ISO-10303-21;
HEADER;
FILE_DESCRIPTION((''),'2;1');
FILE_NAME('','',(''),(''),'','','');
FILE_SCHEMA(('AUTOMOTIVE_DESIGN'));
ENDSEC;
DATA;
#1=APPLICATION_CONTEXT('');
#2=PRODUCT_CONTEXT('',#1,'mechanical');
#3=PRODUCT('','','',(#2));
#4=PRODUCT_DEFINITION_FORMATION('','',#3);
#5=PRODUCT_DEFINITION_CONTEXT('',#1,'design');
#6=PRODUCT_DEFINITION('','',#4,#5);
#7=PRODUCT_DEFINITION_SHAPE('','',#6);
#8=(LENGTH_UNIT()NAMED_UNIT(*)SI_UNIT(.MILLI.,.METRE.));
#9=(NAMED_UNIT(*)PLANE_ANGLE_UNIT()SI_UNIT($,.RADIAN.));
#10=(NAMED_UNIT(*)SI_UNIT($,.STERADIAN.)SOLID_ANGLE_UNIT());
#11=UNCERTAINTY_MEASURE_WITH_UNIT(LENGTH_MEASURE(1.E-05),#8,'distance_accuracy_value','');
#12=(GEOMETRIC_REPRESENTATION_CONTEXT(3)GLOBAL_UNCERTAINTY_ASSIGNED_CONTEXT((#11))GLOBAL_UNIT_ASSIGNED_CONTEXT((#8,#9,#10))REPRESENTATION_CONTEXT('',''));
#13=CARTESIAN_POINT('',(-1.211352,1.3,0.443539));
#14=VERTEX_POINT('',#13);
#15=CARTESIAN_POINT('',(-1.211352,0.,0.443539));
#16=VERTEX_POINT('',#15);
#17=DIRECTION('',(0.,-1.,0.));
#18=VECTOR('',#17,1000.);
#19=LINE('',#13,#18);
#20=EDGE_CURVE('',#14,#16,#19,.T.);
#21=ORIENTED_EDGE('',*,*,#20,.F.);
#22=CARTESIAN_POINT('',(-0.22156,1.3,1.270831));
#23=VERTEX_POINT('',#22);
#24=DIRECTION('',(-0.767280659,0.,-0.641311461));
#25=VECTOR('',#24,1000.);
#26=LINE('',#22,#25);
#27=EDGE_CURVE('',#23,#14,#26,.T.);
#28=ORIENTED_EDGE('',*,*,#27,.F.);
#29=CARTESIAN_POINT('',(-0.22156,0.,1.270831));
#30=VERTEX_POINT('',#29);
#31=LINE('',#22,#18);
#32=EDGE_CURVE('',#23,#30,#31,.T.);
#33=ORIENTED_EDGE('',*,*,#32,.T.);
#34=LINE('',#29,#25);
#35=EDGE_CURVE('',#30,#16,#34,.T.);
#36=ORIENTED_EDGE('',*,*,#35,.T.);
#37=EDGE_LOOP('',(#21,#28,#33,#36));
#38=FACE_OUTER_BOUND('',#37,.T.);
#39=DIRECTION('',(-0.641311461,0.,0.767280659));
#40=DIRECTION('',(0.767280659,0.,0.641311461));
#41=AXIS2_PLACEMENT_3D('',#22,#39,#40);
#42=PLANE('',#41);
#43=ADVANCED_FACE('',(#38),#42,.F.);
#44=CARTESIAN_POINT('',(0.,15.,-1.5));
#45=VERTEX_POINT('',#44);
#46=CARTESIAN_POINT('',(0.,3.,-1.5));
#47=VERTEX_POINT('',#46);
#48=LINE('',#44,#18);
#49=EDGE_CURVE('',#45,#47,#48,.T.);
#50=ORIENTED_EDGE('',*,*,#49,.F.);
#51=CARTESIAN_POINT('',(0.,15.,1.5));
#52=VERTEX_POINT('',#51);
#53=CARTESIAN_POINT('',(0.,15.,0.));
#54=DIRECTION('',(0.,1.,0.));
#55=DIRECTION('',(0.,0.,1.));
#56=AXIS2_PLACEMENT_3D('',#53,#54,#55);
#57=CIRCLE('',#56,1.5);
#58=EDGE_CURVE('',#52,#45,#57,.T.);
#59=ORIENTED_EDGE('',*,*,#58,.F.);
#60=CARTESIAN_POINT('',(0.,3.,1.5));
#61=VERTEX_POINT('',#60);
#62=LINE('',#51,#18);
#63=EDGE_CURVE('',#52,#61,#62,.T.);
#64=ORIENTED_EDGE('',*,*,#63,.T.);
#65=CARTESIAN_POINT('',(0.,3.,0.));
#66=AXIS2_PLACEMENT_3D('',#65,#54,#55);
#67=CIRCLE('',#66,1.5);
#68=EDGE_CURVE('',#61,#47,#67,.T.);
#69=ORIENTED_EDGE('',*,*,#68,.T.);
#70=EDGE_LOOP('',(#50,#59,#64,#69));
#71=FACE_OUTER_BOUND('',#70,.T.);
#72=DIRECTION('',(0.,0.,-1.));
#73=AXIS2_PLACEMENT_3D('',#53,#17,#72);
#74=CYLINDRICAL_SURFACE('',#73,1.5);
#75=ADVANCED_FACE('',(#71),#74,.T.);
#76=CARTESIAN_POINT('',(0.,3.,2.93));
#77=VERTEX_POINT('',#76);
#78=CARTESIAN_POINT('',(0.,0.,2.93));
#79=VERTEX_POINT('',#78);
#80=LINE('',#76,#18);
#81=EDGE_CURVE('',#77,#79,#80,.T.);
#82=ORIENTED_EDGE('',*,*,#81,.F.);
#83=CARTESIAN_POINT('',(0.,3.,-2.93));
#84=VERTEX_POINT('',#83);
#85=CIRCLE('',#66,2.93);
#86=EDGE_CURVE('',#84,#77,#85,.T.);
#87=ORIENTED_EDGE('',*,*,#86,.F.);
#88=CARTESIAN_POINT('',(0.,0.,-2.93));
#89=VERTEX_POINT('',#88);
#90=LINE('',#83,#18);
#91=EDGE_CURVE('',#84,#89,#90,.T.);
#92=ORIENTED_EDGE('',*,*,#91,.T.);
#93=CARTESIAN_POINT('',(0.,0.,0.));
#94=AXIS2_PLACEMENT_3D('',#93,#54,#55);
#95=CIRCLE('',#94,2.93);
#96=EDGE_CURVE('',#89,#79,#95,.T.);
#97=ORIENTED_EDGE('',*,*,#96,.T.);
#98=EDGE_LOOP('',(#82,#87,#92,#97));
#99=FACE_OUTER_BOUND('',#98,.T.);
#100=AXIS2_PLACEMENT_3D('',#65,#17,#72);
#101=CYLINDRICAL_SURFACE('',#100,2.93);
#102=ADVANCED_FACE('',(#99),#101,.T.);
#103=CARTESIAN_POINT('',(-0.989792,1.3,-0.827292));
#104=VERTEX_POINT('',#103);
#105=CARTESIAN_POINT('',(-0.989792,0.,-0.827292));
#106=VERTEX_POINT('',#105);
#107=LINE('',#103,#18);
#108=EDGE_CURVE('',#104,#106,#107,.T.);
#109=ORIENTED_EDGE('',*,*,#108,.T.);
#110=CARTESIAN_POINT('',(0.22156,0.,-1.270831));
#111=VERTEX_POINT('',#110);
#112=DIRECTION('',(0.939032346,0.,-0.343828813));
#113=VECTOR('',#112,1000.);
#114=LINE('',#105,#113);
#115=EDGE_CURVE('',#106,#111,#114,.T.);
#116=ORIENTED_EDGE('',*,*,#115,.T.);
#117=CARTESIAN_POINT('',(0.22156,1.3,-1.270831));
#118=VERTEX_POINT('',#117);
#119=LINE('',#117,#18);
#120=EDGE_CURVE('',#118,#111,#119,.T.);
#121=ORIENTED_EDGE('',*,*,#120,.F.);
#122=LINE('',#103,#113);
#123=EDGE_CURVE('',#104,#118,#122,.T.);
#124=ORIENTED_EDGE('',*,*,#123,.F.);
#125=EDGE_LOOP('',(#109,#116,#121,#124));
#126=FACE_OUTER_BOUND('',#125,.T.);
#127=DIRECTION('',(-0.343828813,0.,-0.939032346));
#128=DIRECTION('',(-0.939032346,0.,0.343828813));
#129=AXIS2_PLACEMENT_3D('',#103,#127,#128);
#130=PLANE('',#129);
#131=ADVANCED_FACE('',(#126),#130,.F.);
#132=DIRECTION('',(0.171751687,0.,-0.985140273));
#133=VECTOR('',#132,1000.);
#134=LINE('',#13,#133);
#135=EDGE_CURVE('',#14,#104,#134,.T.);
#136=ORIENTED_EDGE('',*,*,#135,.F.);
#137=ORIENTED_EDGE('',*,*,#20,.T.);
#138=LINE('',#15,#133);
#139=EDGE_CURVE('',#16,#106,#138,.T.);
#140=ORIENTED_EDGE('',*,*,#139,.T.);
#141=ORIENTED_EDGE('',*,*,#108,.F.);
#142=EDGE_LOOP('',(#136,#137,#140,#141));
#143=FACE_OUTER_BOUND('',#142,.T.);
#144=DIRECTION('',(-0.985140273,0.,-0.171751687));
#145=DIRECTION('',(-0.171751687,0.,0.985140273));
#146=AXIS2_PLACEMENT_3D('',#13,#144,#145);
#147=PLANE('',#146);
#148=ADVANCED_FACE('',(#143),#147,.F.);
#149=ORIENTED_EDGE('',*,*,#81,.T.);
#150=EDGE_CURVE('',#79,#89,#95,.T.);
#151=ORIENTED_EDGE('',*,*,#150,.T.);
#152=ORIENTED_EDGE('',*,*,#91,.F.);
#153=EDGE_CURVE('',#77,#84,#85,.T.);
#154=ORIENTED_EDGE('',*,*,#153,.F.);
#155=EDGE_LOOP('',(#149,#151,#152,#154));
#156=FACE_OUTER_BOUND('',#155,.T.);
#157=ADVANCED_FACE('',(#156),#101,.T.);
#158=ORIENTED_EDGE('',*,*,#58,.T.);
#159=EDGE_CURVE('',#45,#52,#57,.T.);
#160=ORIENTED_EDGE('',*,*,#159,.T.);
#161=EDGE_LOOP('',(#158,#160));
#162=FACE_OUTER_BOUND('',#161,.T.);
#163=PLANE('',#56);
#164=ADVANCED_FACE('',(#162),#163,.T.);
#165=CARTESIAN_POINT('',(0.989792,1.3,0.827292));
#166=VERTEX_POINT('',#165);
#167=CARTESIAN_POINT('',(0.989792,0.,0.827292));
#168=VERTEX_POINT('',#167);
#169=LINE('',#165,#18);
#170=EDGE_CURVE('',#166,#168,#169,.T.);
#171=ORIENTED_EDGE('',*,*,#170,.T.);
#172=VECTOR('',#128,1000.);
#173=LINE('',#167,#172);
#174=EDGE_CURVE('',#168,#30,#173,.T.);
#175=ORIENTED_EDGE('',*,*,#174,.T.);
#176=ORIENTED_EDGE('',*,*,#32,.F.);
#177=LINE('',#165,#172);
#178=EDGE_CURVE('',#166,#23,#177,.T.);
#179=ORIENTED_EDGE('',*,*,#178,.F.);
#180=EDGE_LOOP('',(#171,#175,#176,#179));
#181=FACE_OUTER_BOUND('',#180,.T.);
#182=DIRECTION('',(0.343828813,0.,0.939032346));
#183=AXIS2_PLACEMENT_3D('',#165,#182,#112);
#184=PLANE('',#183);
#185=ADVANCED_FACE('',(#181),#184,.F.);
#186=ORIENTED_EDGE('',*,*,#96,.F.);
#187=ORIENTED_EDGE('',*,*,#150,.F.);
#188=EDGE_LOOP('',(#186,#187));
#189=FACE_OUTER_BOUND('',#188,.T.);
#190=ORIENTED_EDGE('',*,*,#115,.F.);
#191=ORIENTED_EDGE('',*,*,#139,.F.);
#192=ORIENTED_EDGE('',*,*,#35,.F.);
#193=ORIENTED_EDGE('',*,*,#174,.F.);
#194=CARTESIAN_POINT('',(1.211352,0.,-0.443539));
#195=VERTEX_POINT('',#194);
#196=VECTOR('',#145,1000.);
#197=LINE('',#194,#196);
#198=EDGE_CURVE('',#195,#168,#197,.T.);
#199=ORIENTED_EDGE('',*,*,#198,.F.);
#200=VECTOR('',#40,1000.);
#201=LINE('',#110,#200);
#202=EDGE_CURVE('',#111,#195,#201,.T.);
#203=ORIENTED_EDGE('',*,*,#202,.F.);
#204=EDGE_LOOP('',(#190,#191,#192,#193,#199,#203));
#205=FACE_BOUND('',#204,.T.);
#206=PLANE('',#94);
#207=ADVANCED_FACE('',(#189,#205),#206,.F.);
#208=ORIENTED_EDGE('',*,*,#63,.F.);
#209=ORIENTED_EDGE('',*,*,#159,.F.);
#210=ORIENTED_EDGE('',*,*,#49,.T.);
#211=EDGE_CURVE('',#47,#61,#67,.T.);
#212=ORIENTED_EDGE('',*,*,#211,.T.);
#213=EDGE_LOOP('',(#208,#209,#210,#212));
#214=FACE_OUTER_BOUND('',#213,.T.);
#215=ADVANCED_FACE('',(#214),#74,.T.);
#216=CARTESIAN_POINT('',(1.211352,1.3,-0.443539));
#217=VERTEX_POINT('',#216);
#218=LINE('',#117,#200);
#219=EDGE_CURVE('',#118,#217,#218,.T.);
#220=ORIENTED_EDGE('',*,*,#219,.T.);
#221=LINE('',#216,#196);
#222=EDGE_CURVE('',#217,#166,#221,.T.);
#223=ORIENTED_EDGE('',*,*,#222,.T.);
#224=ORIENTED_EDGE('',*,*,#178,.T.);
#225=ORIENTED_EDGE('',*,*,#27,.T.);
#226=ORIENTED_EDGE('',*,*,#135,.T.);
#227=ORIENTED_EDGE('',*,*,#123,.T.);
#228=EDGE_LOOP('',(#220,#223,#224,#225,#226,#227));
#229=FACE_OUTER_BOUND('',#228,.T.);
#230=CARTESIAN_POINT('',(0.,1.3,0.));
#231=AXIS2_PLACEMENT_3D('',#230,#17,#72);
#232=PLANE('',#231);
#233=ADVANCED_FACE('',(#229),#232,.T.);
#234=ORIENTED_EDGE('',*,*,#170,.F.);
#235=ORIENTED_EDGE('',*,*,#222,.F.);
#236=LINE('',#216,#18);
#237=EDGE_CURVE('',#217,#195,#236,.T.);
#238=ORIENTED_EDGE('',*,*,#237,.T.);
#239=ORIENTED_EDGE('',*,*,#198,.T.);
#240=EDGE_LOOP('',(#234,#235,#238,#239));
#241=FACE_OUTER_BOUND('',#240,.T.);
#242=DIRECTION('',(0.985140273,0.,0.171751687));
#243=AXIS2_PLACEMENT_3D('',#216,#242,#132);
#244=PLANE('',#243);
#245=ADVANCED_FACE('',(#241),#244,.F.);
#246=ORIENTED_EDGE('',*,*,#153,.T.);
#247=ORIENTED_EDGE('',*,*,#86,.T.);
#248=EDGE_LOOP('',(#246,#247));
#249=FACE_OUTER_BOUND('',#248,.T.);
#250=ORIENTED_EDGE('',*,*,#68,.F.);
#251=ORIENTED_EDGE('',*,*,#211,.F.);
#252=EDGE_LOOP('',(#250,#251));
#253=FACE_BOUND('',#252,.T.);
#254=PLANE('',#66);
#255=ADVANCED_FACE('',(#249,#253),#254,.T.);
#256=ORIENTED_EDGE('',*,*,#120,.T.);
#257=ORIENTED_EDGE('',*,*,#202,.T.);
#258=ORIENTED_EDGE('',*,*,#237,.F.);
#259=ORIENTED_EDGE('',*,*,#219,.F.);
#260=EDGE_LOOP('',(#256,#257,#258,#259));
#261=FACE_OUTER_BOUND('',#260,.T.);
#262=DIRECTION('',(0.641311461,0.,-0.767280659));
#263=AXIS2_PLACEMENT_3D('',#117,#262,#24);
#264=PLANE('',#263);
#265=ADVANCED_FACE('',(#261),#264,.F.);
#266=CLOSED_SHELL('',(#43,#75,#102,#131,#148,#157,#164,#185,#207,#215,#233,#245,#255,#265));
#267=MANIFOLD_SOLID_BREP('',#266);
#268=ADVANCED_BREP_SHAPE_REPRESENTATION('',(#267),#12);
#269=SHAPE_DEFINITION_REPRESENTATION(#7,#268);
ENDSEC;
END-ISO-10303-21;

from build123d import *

# Parameters (mm, degrees)
SKETCH2_R           = 2.93
BOSS_EXTRUDE1_DEPTH = 3
SKETCH3_R           = 1.5
BOSS_EXTRUDE2_DEPTH = 12
CUT_EXTRUDE1_DEPTH  = 1.3


with BuildPart() as part:
    # Sketch2 → Boss-Extrude1 (new body)
    with BuildSketch(Plane(origin=(0, 0, 0), x_dir=(1, 0, 0), z_dir=(0, 1, 0))):
        with Locations(Location((0, 0, 0), (0, 0, 270))):
            Circle(SKETCH2_R)
    extrude(amount=BOSS_EXTRUDE1_DEPTH)

    # Sketch3 → Boss-Extrude2 (add)
    with BuildSketch(Plane(origin=(0, 3, 0), x_dir=(1, 0, 0), z_dir=(0, 1, 0))):
        with Locations(Location((0, 0, 0), (0, 0, 270))):
            Circle(SKETCH3_R)
    extrude(amount=BOSS_EXTRUDE2_DEPTH)

    # Sketch4 → Cut-Extrude1 (cut)
    with BuildSketch(Plane.XZ):
        Polygon((0.989792051, 0.827291784), (-0.221559676, 1.270830953), (-1.211351727, 0.443539168), (-0.989792051, -0.827291784), (0.221559676, -1.270830953), (1.211351727, -0.443539168), align=None)
    extrude(amount=-CUT_EXTRUDE1_DEPTH, mode=Mode.SUBTRACT)


solid = part.part
